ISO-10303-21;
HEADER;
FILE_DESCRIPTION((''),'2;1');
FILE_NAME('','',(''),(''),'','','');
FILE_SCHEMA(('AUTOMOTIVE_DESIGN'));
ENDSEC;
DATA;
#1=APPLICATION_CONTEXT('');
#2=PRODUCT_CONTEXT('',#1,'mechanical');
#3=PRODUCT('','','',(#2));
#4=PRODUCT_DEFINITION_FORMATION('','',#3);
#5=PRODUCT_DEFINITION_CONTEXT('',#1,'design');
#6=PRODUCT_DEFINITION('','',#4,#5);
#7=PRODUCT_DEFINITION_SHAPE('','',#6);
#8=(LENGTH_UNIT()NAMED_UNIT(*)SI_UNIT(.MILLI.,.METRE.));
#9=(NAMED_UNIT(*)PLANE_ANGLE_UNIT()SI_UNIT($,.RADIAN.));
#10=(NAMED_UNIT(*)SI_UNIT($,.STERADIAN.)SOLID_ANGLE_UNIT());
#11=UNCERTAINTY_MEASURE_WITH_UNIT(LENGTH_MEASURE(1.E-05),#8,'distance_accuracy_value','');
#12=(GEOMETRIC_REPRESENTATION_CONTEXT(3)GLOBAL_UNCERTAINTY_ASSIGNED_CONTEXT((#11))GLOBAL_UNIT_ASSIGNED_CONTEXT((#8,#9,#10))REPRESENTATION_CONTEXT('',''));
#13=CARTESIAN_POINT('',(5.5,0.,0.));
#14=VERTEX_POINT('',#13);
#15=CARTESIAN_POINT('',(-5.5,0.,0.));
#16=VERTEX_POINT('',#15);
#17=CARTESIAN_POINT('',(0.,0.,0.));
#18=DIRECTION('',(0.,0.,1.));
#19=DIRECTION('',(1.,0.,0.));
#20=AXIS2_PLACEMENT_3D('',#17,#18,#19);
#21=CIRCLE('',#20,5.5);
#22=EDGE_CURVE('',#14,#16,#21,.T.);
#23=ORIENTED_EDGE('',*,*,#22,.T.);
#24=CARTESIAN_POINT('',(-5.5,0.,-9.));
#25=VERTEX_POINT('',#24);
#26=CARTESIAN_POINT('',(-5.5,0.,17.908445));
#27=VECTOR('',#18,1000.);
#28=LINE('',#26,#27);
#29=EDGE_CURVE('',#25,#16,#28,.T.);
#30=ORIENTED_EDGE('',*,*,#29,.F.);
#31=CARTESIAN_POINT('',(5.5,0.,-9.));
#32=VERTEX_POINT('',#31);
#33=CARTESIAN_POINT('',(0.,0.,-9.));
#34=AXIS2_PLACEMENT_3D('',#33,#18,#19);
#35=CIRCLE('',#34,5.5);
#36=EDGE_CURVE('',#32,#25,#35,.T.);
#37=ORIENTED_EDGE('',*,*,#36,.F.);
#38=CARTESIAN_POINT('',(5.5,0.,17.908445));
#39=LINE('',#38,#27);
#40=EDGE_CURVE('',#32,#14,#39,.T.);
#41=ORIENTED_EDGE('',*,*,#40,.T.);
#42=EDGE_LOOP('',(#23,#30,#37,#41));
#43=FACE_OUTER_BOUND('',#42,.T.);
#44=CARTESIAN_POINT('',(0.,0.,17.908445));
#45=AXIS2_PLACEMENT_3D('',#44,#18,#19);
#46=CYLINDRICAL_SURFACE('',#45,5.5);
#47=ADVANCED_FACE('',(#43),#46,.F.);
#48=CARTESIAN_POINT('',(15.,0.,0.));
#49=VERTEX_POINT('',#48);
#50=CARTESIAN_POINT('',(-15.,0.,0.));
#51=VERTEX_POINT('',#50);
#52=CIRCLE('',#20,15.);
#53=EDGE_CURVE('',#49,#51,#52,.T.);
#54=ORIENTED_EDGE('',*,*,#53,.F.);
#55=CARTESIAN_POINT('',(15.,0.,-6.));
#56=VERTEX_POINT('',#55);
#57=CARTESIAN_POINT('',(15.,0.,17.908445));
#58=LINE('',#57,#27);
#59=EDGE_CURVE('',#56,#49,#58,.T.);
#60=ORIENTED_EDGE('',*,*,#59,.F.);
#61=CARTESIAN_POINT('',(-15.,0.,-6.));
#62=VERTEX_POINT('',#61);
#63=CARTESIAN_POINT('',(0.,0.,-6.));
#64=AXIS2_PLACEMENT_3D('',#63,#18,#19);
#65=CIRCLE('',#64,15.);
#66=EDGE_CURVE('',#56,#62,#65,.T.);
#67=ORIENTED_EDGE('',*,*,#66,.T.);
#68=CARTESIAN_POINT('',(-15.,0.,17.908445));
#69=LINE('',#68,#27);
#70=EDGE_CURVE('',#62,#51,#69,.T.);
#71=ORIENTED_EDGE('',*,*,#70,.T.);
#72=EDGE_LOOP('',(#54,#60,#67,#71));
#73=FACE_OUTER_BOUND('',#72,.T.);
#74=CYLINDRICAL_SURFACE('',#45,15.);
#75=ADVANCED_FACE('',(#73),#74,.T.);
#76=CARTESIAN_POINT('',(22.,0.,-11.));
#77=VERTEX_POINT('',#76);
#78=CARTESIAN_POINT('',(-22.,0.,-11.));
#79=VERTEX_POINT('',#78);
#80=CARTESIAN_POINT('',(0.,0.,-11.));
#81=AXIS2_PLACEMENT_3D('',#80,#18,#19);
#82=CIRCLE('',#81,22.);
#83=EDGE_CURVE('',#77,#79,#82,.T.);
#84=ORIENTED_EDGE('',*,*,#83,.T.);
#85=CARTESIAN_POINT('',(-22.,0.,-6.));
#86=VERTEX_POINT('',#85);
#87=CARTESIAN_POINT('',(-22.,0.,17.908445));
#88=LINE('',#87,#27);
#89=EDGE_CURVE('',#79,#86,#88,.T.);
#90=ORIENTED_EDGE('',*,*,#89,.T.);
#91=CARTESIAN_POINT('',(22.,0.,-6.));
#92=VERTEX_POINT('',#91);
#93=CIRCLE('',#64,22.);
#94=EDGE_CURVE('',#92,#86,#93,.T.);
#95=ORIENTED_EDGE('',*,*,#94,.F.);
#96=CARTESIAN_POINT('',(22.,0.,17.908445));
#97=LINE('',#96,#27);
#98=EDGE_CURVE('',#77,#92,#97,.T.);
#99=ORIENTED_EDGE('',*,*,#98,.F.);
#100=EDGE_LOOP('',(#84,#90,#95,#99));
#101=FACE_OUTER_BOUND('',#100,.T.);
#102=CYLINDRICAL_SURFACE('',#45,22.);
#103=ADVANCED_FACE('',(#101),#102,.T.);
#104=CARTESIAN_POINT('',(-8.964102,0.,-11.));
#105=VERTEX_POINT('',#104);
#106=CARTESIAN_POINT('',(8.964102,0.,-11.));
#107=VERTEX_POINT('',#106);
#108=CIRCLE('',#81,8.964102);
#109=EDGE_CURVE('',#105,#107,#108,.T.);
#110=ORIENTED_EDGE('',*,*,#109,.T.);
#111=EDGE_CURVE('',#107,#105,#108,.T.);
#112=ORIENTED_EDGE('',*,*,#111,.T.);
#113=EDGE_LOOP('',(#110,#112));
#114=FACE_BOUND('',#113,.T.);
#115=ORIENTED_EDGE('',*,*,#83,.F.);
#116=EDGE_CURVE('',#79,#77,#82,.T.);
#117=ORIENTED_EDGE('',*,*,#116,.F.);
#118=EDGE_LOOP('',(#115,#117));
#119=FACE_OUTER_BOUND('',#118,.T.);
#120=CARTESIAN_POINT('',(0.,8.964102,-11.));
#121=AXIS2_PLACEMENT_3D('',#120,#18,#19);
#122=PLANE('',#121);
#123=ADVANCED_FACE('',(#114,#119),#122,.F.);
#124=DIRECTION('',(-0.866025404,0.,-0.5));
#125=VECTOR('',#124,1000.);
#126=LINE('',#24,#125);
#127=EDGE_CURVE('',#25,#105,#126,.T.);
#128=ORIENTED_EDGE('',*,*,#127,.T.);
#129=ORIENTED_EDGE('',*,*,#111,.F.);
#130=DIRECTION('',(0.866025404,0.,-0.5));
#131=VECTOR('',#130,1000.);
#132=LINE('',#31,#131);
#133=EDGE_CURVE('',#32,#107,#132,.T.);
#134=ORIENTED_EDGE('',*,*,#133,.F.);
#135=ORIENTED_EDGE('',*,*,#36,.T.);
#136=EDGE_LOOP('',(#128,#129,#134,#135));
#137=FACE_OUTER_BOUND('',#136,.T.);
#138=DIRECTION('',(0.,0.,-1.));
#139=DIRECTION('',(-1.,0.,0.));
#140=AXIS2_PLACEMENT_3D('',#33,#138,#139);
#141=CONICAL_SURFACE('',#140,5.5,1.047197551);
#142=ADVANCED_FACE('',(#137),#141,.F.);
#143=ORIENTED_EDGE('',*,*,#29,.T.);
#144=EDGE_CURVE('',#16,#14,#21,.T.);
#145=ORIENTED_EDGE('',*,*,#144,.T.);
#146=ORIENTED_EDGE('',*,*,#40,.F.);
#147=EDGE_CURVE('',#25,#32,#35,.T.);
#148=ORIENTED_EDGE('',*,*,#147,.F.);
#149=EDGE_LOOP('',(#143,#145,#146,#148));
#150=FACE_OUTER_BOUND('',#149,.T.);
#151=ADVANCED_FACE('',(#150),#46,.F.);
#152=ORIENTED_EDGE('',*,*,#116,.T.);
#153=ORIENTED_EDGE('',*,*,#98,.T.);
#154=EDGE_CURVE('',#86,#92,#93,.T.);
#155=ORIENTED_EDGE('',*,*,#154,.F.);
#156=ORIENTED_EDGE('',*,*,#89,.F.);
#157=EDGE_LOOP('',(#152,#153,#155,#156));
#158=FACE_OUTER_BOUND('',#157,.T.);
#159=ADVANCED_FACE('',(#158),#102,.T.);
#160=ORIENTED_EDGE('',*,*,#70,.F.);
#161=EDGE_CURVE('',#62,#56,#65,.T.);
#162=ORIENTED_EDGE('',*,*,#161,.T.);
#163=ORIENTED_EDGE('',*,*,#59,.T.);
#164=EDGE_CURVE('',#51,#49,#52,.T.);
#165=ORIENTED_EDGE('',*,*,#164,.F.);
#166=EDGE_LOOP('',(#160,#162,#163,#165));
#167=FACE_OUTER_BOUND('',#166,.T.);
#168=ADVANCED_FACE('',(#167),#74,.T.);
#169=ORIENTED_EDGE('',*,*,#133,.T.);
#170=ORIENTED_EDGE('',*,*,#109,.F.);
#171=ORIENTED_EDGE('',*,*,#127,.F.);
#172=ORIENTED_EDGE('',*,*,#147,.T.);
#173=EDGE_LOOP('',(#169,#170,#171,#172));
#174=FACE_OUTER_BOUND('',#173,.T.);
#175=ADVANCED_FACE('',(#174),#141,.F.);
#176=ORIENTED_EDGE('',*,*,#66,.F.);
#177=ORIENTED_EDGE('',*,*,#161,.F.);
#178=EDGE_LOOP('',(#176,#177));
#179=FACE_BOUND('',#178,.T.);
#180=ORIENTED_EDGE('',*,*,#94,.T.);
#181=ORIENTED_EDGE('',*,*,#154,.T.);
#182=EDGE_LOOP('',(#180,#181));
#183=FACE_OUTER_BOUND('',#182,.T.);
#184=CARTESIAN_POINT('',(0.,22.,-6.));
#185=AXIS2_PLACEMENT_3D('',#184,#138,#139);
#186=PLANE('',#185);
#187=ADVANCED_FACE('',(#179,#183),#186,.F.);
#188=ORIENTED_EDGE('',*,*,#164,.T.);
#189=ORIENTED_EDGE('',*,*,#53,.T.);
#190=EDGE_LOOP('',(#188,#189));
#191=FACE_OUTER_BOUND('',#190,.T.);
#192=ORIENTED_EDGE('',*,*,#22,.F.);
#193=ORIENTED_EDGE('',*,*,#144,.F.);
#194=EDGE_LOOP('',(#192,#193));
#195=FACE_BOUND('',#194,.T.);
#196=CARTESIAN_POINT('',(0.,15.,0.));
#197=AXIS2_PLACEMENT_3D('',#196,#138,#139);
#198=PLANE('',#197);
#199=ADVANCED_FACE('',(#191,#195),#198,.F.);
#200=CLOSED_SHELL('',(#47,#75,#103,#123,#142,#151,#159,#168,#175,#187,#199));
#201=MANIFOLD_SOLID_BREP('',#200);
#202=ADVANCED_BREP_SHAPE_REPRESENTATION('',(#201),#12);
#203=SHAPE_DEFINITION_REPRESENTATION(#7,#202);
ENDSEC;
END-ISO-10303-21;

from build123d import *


with BuildPart() as part:
    # Sketch1 → Revolve1 (revolve)
    with BuildSketch(Plane(origin=(0, 0, 0), x_dir=(0, 0, -1), z_dir=(1, 0, 0)), mode=Mode.PRIVATE) as revolve1_sk:
        Polygon((0, 15), (0, 5.5), (9, 5.5), (11, 8.964101615), (11, 22), (6, 22), (6, 15), align=None)
    revolve(revolve1_sk.sketch.rotate(Axis((0, 0, 17.908444602), (0, 0, -1)), 90), axis=Axis((0, 0, 17.908444602), (0, 0, -1)))


solid = part.part
